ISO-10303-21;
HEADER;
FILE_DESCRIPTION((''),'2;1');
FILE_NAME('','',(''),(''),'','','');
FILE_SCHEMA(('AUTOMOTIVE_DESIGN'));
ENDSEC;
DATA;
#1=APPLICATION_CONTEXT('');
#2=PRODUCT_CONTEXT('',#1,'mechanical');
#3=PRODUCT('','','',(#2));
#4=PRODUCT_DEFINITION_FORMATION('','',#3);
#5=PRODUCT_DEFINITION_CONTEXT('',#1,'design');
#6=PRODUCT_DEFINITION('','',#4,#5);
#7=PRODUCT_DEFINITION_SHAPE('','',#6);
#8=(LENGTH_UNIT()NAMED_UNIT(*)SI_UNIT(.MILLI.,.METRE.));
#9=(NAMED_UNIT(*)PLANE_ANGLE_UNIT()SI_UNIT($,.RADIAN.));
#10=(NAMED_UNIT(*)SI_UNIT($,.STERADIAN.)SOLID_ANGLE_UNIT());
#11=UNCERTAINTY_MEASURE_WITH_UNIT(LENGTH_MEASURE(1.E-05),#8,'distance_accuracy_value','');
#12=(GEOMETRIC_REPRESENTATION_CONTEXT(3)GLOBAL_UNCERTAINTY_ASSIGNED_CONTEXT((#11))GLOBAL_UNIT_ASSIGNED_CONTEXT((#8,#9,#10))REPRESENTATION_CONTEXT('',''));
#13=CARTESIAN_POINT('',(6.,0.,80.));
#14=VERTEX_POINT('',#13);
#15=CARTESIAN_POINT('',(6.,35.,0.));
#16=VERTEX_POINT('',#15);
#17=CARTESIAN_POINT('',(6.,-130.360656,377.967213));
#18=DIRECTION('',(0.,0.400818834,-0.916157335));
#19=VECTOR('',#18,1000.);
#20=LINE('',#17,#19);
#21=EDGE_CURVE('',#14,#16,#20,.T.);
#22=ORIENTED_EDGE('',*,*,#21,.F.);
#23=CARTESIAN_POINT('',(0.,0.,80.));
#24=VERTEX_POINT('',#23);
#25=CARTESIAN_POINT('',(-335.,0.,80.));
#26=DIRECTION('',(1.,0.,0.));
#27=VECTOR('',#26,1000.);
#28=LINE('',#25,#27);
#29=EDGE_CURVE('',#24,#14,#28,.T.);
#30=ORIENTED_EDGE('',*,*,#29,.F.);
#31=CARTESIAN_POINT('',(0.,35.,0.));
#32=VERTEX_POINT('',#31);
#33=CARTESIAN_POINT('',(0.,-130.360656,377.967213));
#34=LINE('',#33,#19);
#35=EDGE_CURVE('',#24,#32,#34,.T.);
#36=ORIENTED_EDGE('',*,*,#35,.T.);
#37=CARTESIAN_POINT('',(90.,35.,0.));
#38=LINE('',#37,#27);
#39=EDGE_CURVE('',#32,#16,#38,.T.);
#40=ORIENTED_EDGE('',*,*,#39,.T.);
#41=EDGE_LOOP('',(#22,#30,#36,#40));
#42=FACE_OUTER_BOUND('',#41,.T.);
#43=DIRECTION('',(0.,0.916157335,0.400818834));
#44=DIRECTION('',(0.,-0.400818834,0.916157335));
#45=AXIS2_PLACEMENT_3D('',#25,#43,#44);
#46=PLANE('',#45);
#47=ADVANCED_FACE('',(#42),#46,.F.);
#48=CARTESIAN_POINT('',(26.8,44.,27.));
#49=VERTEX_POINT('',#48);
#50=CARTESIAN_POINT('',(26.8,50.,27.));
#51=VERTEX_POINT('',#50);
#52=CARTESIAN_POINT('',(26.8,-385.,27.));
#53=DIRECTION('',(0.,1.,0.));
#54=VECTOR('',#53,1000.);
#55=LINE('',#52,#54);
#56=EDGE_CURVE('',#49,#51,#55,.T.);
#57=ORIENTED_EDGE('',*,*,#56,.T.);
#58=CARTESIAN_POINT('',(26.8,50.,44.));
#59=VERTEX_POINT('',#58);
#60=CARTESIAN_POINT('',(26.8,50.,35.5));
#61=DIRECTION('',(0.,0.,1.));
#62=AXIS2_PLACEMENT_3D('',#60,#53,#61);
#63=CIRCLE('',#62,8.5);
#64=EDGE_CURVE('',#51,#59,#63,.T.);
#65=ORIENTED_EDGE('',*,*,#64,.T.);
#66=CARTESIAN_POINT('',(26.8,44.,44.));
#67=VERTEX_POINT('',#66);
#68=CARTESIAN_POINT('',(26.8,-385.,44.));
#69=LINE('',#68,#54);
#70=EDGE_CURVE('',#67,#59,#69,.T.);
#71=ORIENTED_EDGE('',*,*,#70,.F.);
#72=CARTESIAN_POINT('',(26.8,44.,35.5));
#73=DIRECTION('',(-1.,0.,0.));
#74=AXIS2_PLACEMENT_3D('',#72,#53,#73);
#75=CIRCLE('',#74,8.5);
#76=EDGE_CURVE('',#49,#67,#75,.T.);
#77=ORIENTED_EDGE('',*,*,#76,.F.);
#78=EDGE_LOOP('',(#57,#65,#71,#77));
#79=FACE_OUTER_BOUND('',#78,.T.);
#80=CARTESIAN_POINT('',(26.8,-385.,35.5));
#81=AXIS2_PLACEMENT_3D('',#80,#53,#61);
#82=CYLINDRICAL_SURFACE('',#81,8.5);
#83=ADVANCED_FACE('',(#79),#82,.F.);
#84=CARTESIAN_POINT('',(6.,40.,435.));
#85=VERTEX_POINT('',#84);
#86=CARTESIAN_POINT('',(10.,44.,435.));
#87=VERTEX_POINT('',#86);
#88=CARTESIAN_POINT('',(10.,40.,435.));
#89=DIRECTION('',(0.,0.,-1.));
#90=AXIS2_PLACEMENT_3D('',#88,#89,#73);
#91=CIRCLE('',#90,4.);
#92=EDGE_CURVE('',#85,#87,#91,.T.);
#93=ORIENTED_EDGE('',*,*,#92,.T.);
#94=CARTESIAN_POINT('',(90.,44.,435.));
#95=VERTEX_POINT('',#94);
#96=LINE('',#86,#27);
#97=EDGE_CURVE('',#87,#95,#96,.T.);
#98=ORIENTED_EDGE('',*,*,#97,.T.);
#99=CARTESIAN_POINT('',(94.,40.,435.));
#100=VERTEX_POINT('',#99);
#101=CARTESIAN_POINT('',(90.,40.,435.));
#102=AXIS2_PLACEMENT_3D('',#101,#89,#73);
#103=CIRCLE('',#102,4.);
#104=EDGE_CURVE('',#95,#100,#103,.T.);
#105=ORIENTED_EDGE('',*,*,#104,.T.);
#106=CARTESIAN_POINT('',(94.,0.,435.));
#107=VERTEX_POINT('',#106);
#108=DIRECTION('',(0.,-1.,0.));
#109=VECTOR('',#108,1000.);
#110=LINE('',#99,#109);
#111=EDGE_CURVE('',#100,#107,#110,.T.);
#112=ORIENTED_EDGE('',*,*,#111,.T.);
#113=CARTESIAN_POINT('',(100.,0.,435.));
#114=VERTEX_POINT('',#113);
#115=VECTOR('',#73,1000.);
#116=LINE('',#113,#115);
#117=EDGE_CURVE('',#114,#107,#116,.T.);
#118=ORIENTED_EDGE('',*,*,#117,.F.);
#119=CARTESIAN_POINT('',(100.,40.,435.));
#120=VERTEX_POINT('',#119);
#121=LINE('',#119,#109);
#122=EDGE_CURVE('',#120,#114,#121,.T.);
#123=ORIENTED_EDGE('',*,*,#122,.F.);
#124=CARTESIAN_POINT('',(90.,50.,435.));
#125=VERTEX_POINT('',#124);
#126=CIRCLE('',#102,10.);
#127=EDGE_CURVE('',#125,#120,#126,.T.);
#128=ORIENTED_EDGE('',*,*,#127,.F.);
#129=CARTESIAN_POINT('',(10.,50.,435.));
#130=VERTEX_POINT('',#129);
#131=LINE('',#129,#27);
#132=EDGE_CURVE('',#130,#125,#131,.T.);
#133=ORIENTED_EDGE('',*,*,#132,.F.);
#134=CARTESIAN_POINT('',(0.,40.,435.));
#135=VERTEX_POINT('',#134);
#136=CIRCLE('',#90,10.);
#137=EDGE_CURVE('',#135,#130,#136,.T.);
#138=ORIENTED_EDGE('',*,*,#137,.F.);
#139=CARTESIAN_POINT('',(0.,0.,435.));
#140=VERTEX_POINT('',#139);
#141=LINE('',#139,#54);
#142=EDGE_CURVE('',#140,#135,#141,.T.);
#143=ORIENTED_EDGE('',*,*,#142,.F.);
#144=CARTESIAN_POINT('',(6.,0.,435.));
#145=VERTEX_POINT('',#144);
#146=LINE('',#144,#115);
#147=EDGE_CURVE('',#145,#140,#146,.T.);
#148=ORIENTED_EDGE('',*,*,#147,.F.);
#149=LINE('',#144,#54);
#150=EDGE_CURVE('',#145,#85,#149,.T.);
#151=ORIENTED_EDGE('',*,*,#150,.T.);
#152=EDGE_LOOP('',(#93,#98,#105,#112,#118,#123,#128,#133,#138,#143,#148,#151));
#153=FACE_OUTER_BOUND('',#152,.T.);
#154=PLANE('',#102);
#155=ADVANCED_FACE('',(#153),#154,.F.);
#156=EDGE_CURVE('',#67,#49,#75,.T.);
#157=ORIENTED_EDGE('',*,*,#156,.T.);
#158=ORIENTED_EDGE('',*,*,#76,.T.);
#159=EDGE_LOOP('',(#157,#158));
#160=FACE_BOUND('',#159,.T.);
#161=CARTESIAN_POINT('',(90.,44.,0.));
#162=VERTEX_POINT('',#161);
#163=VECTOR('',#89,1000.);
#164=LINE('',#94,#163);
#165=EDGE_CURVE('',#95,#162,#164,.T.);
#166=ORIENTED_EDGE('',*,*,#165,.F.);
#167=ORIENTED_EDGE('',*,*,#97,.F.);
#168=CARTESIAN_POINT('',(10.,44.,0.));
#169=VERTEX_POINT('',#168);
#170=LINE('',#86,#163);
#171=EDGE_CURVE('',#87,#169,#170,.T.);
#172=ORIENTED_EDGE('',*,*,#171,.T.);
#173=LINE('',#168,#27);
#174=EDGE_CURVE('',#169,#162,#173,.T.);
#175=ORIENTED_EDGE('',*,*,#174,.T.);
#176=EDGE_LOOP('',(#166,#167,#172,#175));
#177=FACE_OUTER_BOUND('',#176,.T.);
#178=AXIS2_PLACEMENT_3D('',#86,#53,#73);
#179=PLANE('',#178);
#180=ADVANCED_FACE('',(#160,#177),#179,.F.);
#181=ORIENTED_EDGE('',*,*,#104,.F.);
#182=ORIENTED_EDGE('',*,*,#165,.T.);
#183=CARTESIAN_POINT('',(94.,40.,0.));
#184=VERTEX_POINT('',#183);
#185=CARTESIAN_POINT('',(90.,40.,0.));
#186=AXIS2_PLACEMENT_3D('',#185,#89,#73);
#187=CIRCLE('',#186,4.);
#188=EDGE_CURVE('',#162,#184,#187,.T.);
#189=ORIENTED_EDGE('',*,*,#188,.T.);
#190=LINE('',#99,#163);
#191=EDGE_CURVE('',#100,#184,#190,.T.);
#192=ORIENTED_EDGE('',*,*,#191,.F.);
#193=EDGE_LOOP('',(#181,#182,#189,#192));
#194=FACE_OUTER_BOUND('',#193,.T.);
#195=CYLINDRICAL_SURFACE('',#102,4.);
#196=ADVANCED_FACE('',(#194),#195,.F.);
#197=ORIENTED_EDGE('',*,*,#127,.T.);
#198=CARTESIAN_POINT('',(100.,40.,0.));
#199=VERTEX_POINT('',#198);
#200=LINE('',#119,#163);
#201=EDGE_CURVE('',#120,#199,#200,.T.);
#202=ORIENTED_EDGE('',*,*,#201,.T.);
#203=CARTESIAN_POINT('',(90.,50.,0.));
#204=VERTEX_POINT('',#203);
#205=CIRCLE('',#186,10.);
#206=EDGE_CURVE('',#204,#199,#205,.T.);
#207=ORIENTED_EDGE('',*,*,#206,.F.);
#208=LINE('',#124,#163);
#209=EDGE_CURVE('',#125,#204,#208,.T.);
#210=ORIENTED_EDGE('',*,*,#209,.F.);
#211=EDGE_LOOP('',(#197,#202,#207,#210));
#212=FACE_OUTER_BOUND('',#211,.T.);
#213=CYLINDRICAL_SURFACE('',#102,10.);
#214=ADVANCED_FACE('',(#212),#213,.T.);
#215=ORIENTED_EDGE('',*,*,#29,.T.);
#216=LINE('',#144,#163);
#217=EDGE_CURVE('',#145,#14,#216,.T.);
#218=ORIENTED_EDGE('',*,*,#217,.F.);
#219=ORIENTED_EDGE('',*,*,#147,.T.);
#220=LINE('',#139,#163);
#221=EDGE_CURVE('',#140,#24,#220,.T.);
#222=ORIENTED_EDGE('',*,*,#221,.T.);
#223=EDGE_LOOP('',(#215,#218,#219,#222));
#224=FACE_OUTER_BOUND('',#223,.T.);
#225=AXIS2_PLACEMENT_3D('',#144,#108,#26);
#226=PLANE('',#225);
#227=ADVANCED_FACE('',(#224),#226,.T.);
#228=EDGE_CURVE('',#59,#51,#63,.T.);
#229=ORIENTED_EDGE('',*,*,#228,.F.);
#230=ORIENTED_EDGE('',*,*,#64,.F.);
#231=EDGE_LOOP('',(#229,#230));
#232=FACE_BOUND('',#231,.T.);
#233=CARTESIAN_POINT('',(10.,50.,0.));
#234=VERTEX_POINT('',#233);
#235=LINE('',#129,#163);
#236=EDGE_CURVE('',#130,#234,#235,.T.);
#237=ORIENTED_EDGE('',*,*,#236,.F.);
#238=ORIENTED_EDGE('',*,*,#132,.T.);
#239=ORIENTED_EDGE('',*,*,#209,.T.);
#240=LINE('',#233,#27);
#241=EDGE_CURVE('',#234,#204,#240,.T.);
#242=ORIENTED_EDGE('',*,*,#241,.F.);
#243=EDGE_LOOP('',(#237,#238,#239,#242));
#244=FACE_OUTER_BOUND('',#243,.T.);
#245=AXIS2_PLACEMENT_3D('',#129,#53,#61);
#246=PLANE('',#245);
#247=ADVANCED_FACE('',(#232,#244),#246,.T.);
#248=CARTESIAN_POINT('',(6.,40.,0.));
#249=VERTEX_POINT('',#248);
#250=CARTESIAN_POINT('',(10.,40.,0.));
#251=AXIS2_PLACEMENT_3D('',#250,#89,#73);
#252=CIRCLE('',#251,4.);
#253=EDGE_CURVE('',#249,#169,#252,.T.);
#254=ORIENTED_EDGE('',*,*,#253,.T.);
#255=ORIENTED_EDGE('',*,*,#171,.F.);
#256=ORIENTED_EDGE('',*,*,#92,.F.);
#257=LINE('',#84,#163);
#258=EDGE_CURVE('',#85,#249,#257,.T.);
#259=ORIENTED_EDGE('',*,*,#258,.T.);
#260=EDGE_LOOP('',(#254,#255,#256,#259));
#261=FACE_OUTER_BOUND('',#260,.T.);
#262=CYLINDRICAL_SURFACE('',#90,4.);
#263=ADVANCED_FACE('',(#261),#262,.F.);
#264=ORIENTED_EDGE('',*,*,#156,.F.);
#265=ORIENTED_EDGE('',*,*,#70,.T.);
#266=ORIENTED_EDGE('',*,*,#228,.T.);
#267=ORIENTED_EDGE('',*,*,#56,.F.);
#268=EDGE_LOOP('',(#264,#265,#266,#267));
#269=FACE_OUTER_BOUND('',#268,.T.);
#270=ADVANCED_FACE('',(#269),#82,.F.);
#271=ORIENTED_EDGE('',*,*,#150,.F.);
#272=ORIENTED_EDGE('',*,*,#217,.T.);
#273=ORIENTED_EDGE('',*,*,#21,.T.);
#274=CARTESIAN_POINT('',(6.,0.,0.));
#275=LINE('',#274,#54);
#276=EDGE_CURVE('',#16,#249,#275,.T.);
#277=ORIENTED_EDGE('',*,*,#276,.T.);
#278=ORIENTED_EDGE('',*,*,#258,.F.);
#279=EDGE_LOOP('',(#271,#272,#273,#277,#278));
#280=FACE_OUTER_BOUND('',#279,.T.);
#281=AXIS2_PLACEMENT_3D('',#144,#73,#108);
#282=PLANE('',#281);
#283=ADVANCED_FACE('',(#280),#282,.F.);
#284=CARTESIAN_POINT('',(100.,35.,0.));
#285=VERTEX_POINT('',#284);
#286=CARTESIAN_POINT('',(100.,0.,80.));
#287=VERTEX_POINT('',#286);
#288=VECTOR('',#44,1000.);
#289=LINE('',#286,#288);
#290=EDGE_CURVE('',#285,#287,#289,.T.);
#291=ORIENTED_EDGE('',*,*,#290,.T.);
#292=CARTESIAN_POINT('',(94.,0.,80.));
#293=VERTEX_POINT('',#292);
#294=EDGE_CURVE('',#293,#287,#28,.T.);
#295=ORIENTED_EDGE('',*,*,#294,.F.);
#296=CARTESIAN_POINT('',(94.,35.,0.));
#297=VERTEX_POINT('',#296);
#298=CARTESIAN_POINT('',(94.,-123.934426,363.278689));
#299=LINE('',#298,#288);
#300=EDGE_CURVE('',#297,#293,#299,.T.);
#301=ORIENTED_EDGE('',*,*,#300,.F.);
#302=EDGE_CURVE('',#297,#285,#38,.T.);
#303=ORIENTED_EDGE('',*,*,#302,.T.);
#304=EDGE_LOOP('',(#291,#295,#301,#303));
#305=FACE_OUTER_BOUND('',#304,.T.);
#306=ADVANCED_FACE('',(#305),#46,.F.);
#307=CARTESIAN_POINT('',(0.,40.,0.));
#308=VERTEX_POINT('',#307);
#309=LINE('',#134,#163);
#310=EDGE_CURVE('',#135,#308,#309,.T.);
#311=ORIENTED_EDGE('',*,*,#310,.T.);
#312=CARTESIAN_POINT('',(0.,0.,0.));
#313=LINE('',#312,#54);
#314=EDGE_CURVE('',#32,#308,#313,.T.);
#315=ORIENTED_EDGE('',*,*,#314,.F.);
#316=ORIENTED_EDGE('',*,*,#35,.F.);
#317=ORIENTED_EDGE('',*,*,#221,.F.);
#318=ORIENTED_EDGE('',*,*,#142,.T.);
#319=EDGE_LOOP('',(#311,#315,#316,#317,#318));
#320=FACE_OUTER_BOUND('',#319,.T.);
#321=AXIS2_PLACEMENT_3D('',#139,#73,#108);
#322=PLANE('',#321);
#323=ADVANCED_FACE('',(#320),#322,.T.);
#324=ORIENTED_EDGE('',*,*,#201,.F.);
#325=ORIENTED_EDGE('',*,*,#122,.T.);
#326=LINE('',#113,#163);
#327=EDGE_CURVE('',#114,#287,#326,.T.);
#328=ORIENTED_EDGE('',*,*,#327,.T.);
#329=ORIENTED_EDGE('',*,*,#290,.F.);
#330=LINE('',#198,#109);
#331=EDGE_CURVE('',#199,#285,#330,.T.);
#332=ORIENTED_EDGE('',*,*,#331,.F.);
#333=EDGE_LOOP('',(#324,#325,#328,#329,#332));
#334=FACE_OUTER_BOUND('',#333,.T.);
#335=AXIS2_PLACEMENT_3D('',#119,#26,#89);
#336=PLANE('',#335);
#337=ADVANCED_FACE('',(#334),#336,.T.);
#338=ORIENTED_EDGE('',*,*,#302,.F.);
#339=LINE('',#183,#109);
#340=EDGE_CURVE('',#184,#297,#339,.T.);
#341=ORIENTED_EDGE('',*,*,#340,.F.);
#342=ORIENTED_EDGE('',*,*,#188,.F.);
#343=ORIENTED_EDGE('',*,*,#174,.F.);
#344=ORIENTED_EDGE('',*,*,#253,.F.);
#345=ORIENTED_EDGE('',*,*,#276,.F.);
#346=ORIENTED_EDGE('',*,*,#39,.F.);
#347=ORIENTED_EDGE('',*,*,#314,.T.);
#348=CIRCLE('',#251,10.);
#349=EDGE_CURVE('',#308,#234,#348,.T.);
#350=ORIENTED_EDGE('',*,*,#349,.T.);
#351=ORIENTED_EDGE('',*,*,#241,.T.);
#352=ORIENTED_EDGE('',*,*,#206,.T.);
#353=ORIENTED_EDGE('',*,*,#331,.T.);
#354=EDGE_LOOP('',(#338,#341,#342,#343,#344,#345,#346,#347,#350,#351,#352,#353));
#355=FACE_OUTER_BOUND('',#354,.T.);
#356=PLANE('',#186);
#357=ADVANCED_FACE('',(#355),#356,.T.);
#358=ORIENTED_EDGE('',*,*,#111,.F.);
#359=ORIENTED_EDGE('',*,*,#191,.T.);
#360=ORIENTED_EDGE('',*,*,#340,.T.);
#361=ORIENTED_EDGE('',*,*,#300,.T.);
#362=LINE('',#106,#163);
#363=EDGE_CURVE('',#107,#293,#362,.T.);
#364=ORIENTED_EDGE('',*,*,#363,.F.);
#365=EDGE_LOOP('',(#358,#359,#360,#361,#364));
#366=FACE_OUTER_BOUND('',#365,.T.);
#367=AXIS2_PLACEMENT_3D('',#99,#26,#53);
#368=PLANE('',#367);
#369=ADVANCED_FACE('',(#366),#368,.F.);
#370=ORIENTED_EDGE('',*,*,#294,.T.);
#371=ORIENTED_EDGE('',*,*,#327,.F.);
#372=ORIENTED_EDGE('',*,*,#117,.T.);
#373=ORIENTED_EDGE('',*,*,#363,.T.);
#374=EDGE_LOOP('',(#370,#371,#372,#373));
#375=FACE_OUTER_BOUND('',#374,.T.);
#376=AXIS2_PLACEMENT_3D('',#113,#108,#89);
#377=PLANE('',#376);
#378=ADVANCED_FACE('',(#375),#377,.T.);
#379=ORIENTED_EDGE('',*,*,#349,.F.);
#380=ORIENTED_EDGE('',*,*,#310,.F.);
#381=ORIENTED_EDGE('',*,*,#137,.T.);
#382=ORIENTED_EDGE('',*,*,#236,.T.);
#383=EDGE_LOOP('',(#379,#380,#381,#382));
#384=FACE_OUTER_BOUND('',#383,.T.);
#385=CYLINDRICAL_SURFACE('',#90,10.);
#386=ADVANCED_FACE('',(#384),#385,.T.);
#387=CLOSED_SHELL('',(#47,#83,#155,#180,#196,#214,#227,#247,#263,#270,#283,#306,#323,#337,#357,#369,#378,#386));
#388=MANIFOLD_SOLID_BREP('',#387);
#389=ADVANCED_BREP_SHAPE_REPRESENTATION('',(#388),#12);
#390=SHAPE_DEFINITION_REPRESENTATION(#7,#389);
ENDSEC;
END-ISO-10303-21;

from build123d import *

# Parameters (mm, degrees)
BOSS_EXTRUDE1_DEPTH = 435
SKETCH2_R           = 8.5
CUT_EXTRUDE1_DEPTH  = 435
CUT_EXTRUDE2_DEPTH  = 435


with BuildPart() as part:
    # Sketch1 → Boss-Extrude1 (new body)
    with BuildSketch(Plane.XY):
        with BuildLine():
            Line((0, 0), (0, 40))
            ThreePointArc((0, 40), (2.928932188, 47.071067812), (10, 50))
            Line((10, 50), (90, 50))
            ThreePointArc((90, 50), (97.071067812, 47.071067812), (100, 40))
            Line((100, 40), (100, 0))
            Line((100, 0), (94, 0))
            Line((94, 0), (94, 40))
            ThreePointArc((94, 40), (92.828427125, 42.828427125), (90, 44))
            Line((90, 44), (10, 44))
            ThreePointArc((10, 44), (7.171572875, 42.828427125), (6, 40))
            Line((6, 40), (6, 0))
            Line((6, 0), (0, 0))
        make_face()
    extrude(amount=BOSS_EXTRUDE1_DEPTH)

    # Sketch2 → Cut-Extrude1 (cut)
    with BuildSketch(Plane(origin=(0, 50, 0), x_dir=(1, 0, 0), z_dir=(0, 1, 0))):
        with Locations(Location((26.8, -35.5, 0), (0, 0, 270))):
            Circle(SKETCH2_R)
    extrude(amount=-CUT_EXTRUDE1_DEPTH, mode=Mode.SUBTRACT)

    # Sketch3 → Cut-Extrude2 (cut)
    with BuildSketch(Plane(origin=(100, 0, 0), x_dir=(0, 0, -1), z_dir=(1, 0, 0))):
        Polygon((-80, 0), (0, 35), (0, 0), align=None)
    extrude(amount=-CUT_EXTRUDE2_DEPTH, mode=Mode.SUBTRACT)


solid = part.part
